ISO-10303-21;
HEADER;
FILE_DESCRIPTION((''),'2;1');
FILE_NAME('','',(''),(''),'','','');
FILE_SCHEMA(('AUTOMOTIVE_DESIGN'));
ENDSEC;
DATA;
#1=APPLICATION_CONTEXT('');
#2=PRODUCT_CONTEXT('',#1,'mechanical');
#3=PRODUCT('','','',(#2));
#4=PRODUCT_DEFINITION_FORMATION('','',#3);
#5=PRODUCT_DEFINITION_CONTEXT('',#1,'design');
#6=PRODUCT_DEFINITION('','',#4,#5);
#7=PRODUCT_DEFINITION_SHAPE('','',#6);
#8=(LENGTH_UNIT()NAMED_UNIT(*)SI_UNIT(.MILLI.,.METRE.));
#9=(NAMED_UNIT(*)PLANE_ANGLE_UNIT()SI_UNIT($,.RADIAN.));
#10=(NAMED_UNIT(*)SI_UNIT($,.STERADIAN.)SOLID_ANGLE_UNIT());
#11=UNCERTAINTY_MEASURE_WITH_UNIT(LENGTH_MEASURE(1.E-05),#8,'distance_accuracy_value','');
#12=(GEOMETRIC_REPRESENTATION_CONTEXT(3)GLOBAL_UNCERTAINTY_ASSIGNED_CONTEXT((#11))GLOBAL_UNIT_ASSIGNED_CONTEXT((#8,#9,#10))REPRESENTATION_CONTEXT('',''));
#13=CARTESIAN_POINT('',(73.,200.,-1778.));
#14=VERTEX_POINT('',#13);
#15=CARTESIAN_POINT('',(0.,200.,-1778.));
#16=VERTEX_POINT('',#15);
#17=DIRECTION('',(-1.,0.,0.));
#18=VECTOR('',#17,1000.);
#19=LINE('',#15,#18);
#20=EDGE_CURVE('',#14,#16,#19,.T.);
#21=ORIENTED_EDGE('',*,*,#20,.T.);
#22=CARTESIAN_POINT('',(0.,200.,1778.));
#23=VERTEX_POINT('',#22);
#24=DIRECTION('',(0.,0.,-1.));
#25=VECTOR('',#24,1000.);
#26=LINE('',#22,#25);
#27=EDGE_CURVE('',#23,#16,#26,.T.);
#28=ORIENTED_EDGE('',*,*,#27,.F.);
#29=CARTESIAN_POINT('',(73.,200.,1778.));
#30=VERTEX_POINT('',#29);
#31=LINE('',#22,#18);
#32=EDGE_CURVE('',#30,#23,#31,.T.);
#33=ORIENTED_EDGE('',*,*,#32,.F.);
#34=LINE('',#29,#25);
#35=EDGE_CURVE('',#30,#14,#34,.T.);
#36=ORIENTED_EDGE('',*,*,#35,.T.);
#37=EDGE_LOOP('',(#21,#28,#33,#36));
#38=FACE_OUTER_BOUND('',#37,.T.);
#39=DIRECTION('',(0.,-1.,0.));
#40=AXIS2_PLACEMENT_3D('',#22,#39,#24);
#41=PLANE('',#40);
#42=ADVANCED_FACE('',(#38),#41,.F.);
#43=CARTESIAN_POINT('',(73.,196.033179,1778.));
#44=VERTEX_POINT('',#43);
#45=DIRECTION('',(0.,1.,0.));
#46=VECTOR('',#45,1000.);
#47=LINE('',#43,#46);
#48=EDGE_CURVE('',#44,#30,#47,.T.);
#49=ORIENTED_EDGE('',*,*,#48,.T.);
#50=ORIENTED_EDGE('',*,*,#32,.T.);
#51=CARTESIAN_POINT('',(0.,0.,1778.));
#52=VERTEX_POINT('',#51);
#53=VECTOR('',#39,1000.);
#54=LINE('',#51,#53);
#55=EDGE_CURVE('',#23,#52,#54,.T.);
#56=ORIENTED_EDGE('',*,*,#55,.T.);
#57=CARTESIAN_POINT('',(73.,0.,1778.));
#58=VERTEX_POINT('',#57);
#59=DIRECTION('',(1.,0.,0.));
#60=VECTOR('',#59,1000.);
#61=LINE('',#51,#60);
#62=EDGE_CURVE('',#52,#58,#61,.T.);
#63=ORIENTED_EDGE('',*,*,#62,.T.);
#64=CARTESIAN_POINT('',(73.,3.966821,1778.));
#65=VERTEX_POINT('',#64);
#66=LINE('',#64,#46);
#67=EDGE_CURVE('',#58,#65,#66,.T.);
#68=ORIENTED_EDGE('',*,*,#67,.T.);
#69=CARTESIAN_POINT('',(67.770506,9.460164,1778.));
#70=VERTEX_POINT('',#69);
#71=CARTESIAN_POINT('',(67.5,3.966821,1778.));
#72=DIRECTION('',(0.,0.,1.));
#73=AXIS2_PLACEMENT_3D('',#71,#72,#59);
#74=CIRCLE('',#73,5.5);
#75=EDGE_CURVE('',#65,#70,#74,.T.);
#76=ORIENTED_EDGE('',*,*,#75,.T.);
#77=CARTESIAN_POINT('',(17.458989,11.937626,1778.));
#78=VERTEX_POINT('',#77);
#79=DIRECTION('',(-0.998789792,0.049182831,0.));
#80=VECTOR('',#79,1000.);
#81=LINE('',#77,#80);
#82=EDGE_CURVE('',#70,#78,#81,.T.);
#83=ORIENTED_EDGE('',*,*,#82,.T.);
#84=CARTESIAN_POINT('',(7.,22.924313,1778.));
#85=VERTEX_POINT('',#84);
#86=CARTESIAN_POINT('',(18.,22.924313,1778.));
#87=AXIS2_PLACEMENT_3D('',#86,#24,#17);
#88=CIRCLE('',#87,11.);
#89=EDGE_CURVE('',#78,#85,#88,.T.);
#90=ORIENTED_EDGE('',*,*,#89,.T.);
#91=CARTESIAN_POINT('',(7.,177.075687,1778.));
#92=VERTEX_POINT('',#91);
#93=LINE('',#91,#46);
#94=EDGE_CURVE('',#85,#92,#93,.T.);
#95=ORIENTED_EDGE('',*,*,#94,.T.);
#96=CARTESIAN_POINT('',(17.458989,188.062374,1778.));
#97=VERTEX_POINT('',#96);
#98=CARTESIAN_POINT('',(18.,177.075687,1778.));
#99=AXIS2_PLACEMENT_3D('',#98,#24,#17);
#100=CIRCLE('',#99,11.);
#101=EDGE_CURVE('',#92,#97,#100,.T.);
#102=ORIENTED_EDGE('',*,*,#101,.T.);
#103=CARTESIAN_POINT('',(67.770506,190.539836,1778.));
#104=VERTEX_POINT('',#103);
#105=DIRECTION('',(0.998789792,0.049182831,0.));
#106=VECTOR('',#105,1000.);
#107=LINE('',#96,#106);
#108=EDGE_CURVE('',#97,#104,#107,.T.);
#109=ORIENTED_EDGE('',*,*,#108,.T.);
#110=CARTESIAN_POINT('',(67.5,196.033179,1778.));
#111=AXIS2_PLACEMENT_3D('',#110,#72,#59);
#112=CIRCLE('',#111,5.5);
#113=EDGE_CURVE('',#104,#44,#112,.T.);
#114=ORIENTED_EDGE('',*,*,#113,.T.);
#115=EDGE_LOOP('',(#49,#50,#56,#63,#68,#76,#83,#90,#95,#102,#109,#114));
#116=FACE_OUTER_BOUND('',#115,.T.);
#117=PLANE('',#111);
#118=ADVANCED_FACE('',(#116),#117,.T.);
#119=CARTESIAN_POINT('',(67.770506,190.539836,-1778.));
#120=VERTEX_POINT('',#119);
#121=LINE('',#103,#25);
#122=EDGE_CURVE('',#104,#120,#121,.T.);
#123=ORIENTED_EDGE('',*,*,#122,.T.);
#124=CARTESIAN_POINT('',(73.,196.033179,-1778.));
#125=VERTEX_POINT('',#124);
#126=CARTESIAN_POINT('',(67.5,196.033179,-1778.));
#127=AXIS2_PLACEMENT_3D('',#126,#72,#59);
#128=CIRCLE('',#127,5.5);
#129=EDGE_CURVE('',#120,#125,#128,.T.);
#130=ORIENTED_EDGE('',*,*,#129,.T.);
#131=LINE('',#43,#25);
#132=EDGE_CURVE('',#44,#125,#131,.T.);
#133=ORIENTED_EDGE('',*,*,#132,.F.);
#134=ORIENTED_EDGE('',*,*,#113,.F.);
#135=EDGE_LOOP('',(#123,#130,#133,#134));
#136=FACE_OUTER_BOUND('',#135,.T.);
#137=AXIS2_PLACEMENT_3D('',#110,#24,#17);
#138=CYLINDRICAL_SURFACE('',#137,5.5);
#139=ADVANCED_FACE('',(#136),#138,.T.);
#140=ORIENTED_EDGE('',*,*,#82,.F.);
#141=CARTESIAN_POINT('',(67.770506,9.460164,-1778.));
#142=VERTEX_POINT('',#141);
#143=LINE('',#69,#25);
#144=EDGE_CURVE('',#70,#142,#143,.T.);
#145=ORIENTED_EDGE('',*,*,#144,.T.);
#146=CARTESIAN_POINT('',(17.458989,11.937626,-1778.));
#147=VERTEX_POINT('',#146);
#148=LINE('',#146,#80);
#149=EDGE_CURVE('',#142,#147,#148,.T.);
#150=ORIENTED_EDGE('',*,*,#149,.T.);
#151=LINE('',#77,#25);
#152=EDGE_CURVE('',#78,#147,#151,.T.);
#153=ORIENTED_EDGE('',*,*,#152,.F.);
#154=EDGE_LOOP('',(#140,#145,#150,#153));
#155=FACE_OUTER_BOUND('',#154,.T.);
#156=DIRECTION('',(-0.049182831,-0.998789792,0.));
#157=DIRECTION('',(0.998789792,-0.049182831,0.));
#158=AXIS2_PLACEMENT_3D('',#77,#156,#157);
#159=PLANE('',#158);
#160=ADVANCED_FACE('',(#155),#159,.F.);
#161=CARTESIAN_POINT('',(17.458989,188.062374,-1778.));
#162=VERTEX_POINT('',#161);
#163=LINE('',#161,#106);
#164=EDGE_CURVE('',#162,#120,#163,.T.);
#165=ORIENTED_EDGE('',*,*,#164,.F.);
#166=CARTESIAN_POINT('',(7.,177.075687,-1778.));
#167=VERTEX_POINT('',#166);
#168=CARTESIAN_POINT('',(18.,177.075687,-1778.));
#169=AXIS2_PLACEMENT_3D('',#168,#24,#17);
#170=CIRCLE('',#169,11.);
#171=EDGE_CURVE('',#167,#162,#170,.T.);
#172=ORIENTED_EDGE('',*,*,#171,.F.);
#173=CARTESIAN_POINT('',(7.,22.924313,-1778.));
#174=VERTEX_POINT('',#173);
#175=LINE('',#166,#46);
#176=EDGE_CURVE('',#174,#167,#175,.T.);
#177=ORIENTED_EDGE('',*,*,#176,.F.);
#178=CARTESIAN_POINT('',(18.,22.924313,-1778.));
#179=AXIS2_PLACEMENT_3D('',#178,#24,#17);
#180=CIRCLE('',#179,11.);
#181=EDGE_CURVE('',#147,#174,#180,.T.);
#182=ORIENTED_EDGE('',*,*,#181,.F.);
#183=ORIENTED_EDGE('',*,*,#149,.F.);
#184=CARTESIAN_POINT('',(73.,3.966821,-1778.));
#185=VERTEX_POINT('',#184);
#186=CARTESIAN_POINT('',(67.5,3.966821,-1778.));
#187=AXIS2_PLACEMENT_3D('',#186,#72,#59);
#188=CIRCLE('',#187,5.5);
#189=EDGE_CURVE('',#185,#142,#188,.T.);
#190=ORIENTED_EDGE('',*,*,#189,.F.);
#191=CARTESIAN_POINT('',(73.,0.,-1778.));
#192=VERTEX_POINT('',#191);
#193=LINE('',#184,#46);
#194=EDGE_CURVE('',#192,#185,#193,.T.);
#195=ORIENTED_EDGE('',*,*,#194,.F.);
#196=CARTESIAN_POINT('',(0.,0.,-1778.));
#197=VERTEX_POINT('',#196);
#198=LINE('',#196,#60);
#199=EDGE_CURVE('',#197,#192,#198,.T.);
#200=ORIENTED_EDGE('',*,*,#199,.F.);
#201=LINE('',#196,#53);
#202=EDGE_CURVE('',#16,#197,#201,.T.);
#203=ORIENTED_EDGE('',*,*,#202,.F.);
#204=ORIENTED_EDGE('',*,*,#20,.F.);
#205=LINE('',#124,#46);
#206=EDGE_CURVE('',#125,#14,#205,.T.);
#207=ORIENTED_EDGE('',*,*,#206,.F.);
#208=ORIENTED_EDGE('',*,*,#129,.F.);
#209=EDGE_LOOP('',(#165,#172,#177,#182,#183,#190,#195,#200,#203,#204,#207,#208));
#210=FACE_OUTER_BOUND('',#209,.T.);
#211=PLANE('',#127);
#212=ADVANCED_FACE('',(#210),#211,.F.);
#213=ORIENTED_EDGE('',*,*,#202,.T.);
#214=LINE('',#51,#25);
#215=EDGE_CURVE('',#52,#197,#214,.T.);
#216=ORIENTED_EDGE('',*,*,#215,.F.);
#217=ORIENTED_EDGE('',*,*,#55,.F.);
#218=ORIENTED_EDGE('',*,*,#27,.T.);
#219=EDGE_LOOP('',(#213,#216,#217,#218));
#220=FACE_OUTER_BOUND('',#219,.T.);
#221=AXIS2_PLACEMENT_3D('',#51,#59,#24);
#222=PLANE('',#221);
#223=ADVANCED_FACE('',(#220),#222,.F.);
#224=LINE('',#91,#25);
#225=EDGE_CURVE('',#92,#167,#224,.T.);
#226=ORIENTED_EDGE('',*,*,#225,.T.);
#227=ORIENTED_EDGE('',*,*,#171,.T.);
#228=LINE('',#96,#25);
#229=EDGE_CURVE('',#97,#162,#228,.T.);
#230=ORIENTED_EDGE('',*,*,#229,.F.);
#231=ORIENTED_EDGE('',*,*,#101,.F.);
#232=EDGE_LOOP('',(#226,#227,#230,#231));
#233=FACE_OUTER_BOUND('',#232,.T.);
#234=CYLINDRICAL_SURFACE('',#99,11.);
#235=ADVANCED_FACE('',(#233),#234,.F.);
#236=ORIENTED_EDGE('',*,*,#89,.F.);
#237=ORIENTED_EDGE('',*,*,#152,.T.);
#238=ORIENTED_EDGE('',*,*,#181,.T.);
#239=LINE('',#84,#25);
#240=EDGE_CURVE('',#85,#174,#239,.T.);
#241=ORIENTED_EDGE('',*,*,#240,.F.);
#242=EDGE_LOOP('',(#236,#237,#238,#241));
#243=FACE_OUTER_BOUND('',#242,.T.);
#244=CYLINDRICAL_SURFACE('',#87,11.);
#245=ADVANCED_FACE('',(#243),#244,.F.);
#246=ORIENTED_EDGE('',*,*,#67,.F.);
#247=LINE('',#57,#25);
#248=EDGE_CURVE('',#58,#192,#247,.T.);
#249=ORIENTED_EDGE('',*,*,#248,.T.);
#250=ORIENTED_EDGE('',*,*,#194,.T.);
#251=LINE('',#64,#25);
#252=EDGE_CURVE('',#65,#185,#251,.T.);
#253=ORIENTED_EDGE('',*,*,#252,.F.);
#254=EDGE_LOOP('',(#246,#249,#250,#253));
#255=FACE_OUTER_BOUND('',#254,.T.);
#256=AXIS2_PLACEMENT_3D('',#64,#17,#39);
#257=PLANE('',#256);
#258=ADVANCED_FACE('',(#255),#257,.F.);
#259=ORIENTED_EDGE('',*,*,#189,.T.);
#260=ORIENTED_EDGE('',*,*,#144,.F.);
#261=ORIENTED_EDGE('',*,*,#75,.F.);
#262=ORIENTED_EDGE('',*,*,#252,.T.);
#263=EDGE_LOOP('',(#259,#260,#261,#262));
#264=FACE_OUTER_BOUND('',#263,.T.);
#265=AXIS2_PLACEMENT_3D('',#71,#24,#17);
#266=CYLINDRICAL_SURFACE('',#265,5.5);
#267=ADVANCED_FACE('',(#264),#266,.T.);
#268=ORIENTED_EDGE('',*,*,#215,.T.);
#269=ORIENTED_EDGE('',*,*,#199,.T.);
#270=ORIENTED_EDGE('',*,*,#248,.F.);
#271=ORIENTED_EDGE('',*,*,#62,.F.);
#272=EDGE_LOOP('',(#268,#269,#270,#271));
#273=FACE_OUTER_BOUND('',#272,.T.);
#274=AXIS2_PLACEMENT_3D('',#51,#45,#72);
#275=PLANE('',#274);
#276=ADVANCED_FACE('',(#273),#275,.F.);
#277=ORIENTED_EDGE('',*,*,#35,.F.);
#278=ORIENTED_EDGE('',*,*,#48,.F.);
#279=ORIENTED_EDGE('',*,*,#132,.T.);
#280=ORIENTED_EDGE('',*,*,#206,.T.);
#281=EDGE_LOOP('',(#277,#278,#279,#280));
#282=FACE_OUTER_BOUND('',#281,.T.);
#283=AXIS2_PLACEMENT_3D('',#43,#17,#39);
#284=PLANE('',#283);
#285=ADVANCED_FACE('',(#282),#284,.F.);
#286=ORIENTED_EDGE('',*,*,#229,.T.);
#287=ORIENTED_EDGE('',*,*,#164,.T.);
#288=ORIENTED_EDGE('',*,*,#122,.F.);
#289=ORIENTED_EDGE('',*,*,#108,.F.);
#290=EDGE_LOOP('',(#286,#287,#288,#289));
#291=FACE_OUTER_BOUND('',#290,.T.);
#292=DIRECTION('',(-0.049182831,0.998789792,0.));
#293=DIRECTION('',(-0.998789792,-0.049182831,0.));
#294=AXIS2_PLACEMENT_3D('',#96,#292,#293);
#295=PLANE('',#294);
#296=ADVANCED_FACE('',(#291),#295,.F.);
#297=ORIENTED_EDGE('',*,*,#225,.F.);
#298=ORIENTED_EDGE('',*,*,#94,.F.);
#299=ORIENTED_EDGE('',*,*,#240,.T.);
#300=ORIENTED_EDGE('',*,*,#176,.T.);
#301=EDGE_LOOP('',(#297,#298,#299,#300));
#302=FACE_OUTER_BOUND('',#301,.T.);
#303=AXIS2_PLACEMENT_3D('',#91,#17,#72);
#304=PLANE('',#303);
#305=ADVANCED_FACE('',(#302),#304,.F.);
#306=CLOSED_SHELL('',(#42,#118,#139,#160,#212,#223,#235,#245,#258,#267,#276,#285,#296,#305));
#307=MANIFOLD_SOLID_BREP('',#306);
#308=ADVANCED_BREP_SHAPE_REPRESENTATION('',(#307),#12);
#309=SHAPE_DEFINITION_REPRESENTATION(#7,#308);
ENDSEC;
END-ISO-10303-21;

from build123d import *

# Parameters (mm, degrees)
BOSS_EXTRUDE1_DEPTH = 1778


with BuildPart() as part:
    # Sketch1 → Boss-Extrude1 (new, symmetric)
    with BuildSketch(Plane(origin=(28.211262136, 0, 0), x_dir=(-1, 0, 0), z_dir=(0, 0, 1))):
        with BuildLine():
            Line((28.211262136, 0), (28.211262136, -200))
            Line((28.211262136, -200), (-44.788737864, -200))
            Line((-44.788737864, -200), (-44.788737864, -196.033179359))
            ThreePointArc((-44.788737864, -196.033179359), (-43.272315441, -192.240936001), (-39.559243433, -190.539835501))
            Line((-39.559243433, -190.539835501), (10.752273273, -188.062374452))
            ThreePointArc((10.752273273, -188.062374452), (18.17841729, -184.660173452), (21.211262136, -177.075686736))
            Line((21.211262136, -177.075686736), (21.211262136, -22.924313264))
            ThreePointArc((21.211262136, -22.924313264), (18.17841729, -15.339826548), (10.752273273, -11.937625548))
            Line((10.752273273, -11.937625548), (-39.559243433, -9.460164499))
            ThreePointArc((-39.559243433, -9.460164499), (-43.272315441, -7.759063999), (-44.788737864, -3.966820641))
            Line((-44.788737864, -3.966820641), (-44.788737864, 0))
            Line((-44.788737864, 0), (28.211262136, 0))
        make_face()
    extrude(amount=BOSS_EXTRUDE1_DEPTH, both=True)


solid = part.part
